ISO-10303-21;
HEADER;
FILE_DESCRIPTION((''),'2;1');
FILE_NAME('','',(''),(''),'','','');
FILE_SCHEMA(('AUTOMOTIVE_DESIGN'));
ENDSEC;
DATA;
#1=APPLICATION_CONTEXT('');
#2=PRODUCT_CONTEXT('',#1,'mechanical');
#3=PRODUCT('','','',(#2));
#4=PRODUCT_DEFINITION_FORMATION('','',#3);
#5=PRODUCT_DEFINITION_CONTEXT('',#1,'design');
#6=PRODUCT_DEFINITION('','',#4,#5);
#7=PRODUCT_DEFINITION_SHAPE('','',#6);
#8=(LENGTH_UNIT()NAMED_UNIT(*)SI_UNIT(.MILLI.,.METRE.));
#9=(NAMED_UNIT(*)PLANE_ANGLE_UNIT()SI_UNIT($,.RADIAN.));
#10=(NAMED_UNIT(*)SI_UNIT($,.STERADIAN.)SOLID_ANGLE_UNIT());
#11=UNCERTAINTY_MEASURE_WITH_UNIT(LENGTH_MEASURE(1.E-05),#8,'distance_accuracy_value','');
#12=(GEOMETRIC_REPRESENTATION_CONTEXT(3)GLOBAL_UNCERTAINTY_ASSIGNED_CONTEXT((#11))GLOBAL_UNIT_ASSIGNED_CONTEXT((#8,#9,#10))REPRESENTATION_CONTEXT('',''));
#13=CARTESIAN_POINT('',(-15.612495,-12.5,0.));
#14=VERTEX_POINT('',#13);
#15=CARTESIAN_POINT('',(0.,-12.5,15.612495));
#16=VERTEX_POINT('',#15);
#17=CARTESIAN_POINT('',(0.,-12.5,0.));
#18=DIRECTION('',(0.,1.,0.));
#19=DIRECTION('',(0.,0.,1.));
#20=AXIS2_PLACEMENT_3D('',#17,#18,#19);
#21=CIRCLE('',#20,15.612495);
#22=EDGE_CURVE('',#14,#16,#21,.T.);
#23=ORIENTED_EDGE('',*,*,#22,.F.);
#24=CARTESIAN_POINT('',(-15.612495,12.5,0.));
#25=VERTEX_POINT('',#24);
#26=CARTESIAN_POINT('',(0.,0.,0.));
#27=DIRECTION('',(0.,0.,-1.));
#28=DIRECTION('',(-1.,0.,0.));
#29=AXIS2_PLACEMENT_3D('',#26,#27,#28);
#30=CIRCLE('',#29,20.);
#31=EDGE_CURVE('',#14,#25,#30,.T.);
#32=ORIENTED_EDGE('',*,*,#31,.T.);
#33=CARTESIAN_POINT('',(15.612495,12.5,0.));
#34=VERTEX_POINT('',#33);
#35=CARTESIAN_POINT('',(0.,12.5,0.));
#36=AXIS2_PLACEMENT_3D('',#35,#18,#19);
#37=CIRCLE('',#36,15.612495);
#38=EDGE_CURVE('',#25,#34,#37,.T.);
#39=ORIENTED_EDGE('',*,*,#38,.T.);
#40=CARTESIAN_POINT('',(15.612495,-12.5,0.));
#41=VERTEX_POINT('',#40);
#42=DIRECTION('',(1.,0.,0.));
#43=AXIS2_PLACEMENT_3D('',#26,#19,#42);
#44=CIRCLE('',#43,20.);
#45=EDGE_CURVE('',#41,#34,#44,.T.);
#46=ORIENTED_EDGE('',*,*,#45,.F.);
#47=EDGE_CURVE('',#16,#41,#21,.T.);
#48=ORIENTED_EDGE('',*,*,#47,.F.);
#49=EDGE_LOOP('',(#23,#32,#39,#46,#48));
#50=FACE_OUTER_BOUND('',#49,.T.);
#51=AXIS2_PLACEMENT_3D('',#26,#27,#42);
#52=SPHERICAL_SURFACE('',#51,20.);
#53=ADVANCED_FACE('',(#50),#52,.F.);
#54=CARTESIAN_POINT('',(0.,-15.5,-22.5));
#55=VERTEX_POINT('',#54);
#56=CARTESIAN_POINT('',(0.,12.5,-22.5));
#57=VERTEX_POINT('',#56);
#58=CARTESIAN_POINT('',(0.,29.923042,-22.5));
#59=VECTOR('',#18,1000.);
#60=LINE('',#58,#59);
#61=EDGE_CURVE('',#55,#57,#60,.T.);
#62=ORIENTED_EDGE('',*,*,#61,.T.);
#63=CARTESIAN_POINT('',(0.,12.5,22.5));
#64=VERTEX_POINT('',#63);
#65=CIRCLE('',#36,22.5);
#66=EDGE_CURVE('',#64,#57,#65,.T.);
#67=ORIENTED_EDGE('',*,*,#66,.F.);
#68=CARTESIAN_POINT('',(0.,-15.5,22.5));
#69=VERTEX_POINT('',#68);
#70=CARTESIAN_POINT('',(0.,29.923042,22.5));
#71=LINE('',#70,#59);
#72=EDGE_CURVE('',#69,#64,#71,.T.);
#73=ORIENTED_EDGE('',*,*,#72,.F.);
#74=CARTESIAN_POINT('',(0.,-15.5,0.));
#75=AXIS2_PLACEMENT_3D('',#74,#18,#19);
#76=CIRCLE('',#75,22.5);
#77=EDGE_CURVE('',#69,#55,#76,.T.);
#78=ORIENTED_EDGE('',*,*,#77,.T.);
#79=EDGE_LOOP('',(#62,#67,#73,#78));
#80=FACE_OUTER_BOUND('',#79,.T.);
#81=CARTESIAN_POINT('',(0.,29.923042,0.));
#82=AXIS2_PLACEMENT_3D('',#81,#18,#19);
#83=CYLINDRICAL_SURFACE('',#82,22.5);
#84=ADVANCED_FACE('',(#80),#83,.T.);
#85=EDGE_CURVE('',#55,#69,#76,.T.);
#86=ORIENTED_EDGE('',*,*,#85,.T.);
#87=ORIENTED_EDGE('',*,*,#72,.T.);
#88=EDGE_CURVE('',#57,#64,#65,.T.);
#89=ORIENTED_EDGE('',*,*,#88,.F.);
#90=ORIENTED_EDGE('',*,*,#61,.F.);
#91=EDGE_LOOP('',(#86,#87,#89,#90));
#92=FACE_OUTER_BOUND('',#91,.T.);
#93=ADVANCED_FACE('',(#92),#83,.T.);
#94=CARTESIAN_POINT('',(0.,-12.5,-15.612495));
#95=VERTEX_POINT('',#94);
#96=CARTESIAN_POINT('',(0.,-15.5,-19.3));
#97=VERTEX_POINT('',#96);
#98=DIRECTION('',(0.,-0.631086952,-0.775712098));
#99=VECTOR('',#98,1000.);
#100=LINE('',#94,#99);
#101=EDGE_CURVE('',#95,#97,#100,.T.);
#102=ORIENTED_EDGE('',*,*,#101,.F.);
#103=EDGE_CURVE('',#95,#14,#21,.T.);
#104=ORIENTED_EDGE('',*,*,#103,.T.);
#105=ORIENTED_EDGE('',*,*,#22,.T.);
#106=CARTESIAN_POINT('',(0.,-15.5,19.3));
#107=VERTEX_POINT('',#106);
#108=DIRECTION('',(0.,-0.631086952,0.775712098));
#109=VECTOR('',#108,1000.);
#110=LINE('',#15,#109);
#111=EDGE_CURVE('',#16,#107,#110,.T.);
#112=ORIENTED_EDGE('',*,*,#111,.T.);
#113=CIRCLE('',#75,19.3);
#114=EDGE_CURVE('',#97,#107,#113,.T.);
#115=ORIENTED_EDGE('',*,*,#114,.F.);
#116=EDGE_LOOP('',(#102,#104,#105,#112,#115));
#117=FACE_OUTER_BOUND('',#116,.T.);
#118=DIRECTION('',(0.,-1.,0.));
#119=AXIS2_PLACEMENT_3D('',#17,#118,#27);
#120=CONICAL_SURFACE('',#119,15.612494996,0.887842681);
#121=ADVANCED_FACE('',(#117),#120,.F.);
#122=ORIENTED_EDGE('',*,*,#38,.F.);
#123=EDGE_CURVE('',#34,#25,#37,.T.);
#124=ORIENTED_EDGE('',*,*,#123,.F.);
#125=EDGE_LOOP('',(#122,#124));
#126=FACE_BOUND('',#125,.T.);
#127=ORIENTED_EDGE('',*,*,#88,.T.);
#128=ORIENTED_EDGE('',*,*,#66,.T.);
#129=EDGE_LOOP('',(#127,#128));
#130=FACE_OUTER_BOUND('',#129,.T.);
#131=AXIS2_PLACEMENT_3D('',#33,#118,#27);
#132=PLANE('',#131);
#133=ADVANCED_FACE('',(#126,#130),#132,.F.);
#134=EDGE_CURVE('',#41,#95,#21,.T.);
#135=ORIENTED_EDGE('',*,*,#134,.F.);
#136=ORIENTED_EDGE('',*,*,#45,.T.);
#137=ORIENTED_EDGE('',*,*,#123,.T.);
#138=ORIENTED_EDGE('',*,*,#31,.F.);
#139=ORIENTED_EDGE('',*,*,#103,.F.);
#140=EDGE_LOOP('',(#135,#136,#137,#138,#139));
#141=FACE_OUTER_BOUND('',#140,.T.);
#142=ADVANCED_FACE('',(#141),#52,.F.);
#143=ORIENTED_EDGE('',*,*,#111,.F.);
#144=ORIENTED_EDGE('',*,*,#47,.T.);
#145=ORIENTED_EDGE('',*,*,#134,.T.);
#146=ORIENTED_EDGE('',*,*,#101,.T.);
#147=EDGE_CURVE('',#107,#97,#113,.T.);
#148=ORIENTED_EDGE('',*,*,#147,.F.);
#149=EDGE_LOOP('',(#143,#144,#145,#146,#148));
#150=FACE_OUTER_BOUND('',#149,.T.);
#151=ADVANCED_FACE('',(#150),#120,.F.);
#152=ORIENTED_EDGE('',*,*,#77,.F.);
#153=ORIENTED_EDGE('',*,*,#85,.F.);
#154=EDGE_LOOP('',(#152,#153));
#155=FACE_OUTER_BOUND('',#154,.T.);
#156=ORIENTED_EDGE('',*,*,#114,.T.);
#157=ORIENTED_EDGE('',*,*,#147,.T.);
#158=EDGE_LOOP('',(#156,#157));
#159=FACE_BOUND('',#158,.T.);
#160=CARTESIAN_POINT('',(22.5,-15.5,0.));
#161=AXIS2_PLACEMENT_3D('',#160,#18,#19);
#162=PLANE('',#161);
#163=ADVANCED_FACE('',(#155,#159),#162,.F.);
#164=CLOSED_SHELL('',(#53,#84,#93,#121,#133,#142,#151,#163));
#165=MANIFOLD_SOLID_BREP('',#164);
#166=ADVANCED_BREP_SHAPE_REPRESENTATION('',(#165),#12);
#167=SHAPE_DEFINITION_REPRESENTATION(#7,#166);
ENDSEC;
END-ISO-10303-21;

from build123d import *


with BuildPart() as part:
    # 草图1 → 旋转1 (revolve)
    with BuildSketch(Plane.XY):
        with BuildLine():
            Line((15.612494996, 12.5), (22.5, 12.5))
            Line((22.5, 12.5), (22.5, -15.5))
            Line((22.5, -15.5), (19.3, -15.5))
            Line((19.3, -15.5), (15.612494996, -12.5))
            ThreePointArc((15.612494996, -12.5), (20, 0), (15.612494996, 12.5))
        make_face()
    revolve(axis=Axis((0, 29.923042414, 0), (0, -1, 0)))


solid = part.part
